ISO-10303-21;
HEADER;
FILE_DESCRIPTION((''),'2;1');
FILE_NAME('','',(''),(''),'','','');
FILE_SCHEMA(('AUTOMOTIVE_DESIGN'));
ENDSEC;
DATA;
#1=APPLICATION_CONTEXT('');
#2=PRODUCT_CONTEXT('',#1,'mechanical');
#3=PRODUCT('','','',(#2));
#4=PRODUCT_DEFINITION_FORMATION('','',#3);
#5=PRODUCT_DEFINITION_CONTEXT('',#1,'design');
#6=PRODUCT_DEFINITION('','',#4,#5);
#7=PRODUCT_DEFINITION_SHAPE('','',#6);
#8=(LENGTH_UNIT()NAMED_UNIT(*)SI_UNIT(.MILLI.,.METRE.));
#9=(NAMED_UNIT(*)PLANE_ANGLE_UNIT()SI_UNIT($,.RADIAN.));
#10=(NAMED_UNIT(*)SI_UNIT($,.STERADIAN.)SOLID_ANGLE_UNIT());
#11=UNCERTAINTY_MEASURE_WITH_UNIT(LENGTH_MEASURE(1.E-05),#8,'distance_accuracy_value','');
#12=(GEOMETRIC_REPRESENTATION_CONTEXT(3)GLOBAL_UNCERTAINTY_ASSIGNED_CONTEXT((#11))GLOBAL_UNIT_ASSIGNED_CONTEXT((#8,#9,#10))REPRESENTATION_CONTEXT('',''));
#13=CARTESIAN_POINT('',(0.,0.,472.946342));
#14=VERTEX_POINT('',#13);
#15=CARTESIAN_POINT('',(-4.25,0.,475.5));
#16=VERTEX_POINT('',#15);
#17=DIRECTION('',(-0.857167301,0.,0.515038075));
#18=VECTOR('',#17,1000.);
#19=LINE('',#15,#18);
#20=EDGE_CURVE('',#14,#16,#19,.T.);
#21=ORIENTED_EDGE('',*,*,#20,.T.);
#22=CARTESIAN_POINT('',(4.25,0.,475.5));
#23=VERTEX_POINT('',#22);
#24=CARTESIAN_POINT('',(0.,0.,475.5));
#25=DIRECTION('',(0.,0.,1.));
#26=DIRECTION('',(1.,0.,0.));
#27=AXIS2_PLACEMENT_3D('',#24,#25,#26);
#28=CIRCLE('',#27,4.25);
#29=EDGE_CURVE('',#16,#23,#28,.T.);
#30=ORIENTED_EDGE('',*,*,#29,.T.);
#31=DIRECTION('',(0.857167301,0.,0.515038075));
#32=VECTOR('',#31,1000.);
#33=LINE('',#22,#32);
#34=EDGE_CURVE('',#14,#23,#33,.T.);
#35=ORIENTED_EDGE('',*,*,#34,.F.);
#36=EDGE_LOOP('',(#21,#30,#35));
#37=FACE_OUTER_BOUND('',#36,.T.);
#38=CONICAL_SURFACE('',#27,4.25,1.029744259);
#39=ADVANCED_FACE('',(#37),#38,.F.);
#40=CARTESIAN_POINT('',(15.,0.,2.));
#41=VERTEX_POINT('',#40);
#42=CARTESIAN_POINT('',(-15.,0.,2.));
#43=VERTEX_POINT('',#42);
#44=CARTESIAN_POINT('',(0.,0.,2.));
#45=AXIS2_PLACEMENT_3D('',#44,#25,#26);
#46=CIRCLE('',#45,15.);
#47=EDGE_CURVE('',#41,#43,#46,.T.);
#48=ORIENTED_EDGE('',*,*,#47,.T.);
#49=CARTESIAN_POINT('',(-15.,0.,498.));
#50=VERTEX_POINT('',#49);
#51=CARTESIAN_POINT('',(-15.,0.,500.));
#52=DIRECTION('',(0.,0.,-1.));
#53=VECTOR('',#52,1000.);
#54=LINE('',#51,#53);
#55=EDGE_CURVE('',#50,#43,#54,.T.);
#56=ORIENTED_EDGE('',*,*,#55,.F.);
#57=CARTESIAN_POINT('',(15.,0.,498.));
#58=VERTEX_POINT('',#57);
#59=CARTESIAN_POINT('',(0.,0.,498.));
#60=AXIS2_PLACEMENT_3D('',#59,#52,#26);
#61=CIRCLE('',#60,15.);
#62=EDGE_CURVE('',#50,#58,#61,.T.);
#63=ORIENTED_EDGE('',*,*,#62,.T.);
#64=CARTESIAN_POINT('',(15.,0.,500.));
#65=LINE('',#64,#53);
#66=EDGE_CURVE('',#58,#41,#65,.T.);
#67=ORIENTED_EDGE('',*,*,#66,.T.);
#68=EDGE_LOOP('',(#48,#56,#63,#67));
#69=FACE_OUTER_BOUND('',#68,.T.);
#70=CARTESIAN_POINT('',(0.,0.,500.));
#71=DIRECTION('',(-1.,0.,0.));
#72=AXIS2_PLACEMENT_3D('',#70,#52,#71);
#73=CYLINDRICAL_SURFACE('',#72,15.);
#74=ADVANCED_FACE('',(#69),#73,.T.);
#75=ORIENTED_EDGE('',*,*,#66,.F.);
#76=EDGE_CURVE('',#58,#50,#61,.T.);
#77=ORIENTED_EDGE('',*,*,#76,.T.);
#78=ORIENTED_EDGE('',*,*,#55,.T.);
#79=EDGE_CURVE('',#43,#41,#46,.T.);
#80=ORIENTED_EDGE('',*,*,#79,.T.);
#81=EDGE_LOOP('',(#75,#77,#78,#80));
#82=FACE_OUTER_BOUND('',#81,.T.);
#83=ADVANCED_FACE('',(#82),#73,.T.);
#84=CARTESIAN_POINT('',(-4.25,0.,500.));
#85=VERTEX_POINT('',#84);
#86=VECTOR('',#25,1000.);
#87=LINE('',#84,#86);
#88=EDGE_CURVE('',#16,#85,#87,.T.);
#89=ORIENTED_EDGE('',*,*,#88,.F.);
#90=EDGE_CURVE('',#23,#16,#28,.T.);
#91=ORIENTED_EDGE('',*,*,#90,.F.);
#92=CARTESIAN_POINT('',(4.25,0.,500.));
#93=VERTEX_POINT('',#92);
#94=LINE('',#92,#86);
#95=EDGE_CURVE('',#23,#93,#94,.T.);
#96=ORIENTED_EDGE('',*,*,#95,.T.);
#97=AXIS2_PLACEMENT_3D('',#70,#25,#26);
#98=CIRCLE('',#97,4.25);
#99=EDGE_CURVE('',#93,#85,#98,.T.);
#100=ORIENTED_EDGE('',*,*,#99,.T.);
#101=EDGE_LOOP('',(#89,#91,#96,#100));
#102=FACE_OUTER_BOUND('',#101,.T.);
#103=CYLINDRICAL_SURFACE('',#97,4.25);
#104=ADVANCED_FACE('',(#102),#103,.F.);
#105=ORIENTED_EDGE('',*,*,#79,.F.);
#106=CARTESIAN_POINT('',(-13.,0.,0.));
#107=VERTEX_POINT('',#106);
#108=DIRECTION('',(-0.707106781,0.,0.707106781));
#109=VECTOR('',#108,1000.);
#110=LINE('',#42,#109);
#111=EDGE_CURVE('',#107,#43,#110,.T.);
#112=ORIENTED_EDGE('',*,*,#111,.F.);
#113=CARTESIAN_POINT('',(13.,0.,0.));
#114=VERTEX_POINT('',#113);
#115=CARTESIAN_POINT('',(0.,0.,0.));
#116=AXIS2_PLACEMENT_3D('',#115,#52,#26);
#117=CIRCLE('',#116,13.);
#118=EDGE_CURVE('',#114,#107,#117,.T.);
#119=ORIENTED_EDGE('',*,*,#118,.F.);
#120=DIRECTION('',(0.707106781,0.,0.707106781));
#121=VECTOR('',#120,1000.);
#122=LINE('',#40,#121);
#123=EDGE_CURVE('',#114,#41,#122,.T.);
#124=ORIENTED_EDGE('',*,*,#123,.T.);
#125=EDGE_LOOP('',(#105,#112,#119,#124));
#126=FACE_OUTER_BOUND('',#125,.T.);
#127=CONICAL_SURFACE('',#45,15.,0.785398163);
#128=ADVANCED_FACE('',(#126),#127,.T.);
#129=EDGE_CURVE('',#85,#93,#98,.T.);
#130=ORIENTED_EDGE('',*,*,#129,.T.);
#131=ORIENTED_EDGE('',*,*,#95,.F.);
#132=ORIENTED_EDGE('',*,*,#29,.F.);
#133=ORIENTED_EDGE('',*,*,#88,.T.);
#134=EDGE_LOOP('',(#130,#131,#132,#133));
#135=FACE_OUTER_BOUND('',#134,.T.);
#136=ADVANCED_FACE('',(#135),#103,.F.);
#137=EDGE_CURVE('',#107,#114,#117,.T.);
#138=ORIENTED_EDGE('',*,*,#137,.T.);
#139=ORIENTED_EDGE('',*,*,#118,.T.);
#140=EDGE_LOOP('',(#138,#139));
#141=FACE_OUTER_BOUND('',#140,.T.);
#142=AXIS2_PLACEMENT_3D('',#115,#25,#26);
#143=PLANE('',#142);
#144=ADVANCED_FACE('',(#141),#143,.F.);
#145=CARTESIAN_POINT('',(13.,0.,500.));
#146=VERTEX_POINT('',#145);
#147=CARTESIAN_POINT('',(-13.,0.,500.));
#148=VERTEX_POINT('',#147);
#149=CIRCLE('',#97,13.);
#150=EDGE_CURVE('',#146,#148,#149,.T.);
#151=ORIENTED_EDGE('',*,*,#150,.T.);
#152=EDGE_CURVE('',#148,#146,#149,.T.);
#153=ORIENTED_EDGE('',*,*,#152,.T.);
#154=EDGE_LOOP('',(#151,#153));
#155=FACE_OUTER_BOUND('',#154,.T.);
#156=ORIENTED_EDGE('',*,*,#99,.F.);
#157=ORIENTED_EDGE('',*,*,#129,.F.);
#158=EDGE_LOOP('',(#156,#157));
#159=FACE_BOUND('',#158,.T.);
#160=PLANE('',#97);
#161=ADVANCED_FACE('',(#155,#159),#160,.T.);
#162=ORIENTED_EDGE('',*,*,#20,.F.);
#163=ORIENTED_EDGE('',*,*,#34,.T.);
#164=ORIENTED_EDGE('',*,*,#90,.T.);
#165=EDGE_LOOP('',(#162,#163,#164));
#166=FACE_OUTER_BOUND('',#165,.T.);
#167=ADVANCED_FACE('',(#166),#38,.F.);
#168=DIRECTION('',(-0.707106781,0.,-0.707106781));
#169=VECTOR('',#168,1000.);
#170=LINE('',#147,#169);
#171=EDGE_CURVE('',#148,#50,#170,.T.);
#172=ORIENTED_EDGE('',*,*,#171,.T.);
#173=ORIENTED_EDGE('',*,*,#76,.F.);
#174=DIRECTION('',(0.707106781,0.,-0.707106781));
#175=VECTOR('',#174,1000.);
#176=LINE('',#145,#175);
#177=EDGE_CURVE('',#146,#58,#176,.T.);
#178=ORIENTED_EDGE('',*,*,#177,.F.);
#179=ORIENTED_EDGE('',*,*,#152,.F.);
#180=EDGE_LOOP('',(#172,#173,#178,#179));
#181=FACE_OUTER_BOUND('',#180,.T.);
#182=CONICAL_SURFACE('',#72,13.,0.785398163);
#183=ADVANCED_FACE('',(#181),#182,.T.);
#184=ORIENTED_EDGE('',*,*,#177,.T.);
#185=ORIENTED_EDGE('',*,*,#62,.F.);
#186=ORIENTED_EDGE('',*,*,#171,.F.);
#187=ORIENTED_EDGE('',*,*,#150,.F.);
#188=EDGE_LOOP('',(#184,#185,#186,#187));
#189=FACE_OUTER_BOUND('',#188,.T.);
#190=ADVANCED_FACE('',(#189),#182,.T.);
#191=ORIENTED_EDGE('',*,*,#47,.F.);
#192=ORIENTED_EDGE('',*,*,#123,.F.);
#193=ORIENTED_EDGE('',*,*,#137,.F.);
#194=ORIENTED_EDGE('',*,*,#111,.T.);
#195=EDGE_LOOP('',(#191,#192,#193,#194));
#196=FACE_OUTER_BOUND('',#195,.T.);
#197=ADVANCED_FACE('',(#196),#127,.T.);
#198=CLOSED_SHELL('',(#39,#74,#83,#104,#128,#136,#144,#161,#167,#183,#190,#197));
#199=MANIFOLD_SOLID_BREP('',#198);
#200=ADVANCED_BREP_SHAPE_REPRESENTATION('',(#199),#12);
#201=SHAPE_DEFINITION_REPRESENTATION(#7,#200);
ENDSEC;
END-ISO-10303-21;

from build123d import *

# Parameters (mm, degrees)
SKETCH1_R              = 15
BOSS_EXTRUDE1_DEPTH    = 500
CHAMFER1_SIZE          = 2
M10_TAPPED_HOLE1_D     = 8.5
M10_TAPPED_HOLE1_DEPTH = 24.5
M10_TAPPED_HOLE1_TIP   = 2.553657631


with BuildPart() as part:
    # Sketch1 → Boss-Extrude1 (new body)
    with BuildSketch(Plane.XY):
        Circle(SKETCH1_R)
    extrude(amount=BOSS_EXTRUDE1_DEPTH)

    # Chamfer1
    chamfer1_edges = [part.edges().sort_by_distance(p)[0] for p in [
        (-15, 0, 0),
        (-15, 0, 500),
    ]]
    chamfer(chamfer1_edges, length=CHAMFER1_SIZE)

    # M10 Tapped Hole1
    with Locations(Plane.XY.offset(500)):
        with Locations((0, 0)):
            Hole(M10_TAPPED_HOLE1_D / 2, depth=M10_TAPPED_HOLE1_DEPTH)
            with Locations((0, 0, -(M10_TAPPED_HOLE1_DEPTH + M10_TAPPED_HOLE1_TIP / 2))):  # 118° drill point
                Cone(0, M10_TAPPED_HOLE1_D / 2, M10_TAPPED_HOLE1_TIP, mode=Mode.SUBTRACT)


solid = part.part
